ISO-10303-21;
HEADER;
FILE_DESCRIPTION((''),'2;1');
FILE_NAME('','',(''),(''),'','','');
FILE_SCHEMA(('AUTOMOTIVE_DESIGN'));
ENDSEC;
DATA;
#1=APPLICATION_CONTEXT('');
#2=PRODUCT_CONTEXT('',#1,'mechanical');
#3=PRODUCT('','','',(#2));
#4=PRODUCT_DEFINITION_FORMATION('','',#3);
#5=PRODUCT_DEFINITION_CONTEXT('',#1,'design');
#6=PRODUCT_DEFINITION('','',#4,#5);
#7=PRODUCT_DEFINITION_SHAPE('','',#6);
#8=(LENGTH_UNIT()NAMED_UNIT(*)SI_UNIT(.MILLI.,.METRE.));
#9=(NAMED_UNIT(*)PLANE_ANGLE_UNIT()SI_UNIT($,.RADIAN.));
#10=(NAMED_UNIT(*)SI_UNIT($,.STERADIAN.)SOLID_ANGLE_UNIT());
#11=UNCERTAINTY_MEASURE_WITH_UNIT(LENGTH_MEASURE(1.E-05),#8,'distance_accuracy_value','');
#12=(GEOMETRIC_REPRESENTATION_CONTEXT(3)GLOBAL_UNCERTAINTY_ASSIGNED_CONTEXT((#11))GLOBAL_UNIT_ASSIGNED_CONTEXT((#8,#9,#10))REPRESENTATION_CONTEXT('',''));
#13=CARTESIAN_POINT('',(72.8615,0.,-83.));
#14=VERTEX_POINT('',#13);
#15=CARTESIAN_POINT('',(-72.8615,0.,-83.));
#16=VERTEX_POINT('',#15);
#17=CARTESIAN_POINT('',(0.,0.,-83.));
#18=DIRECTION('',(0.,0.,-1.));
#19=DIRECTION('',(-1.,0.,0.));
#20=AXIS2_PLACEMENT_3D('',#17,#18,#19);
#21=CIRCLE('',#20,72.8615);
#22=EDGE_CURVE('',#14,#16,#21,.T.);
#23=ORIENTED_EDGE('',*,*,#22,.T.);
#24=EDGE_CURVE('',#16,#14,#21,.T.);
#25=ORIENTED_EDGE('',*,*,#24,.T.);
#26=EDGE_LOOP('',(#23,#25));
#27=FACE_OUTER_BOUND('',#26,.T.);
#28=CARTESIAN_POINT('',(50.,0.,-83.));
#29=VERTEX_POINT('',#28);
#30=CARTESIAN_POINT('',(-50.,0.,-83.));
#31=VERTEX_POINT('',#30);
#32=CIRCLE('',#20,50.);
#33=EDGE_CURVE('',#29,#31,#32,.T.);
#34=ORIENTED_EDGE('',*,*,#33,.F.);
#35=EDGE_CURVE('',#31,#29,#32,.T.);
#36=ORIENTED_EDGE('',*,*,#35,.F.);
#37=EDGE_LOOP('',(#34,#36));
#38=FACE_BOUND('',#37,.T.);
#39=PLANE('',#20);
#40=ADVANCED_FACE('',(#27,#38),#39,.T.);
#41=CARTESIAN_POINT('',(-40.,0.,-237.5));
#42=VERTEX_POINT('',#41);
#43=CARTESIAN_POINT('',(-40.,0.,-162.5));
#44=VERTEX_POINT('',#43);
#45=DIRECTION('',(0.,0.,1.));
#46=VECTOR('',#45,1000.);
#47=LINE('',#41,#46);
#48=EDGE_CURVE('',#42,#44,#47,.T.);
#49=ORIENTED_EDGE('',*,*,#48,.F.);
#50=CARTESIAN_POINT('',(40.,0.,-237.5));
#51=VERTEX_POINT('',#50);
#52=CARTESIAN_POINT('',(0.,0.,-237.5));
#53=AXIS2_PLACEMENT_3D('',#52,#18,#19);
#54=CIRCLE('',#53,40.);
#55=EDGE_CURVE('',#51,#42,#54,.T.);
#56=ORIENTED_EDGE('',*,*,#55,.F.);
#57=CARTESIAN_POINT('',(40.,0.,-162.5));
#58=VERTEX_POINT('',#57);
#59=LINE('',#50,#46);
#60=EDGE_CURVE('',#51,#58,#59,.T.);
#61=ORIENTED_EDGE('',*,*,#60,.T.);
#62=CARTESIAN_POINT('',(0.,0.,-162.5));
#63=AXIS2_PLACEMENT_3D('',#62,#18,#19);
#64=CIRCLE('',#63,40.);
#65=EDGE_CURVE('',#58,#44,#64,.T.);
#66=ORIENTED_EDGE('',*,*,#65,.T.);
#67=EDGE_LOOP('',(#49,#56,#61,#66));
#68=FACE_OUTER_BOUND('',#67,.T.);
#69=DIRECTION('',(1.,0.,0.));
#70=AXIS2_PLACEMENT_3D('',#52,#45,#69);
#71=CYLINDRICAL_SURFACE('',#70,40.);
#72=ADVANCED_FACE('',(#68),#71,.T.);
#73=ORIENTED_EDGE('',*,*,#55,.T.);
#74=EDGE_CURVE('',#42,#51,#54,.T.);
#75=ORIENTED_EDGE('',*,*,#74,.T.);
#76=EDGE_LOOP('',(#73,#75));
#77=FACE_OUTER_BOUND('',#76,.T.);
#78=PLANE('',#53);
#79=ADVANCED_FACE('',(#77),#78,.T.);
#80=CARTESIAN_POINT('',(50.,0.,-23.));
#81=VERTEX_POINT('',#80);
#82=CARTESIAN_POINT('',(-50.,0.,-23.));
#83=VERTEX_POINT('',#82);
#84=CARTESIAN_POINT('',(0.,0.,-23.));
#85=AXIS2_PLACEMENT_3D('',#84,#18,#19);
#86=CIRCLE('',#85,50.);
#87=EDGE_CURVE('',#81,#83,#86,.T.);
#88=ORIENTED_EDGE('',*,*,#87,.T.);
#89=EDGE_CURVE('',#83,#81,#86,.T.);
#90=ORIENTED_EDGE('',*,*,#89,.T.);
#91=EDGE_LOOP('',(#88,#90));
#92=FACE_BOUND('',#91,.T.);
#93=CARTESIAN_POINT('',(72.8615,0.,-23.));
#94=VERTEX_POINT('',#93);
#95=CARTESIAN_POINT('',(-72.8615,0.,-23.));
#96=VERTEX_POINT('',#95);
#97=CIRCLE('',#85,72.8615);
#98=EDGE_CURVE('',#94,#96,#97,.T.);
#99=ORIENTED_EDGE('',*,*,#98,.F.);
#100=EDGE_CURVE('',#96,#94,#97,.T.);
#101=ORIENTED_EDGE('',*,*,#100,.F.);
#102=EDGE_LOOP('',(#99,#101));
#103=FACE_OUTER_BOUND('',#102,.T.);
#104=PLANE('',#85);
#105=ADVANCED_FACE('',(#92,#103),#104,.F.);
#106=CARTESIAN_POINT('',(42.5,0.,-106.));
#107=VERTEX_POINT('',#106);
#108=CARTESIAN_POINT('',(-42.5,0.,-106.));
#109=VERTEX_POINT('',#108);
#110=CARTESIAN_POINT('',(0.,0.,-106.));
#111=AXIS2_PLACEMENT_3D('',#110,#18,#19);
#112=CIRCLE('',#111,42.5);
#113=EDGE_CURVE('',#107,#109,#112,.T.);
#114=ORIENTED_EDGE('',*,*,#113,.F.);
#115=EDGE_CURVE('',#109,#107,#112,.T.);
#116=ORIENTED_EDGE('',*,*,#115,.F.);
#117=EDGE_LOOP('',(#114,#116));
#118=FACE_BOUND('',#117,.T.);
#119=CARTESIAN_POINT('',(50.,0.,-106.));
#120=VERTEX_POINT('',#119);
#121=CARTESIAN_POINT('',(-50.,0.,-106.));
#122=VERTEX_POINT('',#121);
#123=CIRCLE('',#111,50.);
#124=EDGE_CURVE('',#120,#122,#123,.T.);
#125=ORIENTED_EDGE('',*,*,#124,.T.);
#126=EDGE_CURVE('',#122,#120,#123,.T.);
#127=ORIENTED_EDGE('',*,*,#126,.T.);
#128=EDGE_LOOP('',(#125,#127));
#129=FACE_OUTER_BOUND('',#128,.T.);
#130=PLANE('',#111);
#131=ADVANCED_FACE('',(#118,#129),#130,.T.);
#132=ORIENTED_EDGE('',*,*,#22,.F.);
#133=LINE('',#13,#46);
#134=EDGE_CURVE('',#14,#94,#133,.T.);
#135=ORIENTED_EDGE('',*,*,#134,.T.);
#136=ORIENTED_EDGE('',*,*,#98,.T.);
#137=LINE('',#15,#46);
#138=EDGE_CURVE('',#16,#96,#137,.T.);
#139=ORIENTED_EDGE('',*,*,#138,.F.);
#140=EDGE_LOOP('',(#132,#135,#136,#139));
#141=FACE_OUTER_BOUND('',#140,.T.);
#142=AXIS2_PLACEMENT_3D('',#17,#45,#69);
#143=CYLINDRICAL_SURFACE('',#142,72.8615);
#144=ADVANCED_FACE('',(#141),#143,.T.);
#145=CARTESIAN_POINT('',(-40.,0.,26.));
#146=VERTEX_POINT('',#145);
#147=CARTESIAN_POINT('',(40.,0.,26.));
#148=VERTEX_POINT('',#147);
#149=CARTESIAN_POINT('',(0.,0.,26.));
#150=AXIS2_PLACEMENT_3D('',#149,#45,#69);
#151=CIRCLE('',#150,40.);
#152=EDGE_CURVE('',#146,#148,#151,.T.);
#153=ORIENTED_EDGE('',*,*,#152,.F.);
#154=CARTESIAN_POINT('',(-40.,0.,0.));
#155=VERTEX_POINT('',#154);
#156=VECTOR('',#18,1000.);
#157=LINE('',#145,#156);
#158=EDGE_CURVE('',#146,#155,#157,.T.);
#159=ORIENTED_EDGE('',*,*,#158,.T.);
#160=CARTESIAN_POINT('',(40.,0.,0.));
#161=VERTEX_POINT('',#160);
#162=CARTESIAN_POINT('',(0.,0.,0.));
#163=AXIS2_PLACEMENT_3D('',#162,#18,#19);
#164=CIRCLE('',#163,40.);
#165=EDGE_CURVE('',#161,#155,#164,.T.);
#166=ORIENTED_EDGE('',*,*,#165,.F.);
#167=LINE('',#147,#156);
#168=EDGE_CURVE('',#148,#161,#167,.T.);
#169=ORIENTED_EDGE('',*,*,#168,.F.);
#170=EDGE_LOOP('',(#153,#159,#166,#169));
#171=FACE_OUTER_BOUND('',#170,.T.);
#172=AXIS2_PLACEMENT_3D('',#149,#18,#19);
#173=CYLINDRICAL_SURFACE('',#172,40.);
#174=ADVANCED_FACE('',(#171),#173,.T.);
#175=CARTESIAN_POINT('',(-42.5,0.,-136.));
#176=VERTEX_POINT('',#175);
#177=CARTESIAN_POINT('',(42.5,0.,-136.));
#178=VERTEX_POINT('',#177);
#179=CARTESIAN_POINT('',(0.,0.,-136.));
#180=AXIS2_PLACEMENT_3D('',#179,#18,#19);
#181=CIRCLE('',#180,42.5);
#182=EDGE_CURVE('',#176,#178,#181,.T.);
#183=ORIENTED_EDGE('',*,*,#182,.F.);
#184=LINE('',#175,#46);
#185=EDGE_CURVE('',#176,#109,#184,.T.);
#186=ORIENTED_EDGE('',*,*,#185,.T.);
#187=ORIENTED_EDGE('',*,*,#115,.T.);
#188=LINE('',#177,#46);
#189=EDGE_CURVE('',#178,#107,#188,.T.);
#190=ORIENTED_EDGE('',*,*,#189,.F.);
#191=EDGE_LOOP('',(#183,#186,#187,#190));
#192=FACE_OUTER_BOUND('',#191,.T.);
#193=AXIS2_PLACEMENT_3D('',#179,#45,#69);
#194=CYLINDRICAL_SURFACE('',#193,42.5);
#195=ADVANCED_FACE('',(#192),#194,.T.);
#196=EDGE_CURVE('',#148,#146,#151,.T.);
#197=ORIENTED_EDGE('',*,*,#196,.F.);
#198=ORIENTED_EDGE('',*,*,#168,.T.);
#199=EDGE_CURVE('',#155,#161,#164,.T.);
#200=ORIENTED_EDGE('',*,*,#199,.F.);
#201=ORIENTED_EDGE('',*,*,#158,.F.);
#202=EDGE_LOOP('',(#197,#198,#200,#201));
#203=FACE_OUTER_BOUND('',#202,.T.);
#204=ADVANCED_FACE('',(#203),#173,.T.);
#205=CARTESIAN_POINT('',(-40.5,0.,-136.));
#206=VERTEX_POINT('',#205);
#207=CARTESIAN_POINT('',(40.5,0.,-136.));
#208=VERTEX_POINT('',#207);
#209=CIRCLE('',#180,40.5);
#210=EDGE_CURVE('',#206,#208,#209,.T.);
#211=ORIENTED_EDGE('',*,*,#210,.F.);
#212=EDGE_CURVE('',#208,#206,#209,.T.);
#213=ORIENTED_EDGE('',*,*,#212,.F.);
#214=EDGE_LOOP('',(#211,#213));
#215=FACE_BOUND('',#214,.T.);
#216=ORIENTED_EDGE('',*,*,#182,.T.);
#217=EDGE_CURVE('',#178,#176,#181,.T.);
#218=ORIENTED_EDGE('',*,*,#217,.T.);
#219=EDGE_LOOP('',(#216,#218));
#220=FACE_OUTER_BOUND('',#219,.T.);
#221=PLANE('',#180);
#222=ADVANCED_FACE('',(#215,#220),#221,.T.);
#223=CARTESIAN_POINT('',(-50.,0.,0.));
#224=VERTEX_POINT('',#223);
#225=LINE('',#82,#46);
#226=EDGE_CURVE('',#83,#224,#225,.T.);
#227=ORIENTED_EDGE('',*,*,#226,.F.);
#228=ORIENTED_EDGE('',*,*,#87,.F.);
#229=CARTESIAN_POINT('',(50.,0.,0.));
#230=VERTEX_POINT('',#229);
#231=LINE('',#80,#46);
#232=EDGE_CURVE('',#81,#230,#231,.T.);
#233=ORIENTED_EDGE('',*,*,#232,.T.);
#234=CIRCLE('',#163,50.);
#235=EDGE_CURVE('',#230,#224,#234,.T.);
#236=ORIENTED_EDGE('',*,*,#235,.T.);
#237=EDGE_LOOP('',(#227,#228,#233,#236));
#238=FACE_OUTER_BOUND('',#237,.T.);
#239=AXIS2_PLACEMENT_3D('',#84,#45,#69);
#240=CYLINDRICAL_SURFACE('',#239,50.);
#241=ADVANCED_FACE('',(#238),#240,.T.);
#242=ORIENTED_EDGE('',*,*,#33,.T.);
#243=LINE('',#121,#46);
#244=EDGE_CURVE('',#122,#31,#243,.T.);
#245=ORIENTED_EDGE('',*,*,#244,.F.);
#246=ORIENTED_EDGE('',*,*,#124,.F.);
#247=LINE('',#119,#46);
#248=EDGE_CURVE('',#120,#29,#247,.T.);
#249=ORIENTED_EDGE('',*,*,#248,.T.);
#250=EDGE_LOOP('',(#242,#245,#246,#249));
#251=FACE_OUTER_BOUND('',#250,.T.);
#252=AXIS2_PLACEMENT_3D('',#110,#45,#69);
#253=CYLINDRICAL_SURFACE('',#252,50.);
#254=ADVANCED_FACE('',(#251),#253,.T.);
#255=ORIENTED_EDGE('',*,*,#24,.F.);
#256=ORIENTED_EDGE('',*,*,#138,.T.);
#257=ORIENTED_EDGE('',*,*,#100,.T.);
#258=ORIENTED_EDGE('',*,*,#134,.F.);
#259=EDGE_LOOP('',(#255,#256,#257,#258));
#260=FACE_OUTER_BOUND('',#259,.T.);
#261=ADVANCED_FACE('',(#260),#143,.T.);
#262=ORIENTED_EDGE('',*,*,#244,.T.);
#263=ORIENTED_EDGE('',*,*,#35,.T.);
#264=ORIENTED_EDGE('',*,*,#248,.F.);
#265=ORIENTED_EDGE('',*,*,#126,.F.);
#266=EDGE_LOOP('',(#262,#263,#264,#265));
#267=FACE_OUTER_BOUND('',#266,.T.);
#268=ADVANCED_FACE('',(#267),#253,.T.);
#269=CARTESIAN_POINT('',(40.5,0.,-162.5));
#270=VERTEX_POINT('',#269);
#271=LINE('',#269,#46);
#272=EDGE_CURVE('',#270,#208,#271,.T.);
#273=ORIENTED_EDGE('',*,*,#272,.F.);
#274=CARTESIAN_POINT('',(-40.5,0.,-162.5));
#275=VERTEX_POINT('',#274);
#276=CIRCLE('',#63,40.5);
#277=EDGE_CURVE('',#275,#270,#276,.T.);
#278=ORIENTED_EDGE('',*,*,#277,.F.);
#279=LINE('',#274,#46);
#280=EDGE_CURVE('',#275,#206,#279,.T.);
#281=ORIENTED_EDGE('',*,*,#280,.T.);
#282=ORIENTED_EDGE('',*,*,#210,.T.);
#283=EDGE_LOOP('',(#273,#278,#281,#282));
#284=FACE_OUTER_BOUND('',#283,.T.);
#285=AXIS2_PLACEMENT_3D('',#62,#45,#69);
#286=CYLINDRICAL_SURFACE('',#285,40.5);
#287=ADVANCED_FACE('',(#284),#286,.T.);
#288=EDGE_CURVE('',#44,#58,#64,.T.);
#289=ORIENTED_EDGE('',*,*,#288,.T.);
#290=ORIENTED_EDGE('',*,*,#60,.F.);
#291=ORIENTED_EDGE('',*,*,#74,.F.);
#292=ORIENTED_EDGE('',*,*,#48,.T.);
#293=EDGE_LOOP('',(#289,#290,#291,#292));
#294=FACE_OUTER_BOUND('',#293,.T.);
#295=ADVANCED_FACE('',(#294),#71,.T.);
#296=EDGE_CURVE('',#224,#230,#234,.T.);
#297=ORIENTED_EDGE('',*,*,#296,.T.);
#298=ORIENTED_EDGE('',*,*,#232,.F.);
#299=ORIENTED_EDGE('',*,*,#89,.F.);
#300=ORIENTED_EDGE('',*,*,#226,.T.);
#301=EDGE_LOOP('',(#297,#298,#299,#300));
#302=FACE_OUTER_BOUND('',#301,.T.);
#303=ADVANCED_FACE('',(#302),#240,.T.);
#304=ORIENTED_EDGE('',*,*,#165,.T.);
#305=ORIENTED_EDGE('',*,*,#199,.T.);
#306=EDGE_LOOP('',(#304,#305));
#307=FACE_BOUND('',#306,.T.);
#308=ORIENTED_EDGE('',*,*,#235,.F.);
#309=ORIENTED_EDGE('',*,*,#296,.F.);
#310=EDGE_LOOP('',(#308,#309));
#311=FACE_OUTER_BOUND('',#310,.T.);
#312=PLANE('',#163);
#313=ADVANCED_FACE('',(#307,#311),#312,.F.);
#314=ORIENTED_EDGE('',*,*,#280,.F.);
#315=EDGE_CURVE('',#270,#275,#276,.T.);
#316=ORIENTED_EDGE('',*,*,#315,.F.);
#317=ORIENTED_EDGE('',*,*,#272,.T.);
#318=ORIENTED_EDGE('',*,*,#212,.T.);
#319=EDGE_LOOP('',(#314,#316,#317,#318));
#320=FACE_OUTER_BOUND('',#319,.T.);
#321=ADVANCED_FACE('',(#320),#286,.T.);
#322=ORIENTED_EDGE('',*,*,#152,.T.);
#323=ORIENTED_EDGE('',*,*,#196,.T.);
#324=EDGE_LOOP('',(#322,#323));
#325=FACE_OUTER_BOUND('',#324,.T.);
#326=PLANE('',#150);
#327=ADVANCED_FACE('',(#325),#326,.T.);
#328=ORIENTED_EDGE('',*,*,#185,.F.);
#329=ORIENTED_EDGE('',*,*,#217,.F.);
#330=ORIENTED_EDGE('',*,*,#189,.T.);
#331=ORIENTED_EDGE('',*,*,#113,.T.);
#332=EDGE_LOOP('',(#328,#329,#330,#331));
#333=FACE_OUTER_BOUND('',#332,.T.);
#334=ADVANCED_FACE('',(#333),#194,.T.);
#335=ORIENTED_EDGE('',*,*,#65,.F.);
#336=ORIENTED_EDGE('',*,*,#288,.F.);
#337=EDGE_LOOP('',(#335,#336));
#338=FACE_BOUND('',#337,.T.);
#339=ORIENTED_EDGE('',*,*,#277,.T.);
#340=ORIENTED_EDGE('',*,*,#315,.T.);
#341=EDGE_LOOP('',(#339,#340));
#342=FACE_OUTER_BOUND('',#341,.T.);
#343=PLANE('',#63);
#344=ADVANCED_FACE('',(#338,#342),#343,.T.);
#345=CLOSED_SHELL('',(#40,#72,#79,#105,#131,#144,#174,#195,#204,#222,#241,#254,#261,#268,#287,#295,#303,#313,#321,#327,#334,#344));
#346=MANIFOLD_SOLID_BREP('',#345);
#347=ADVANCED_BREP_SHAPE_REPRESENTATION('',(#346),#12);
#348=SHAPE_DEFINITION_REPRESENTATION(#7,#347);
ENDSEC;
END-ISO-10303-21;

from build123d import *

# Parameters (mm, degrees)
SKETCH1_R           = 40
BOSS_EXTRUDE1_DEPTH = 26
SKETCH2_R           = 50
BOSS_EXTRUDE2_DEPTH = 23
SKETCH3_R           = 72.8615
BOSS_EXTRUDE3_DEPTH = 60
SKETCH4_R           = 50
BOSS_EXTRUDE4_DEPTH = 23
SKETCH6_R           = 42.5
BOSS_EXTRUDE5_DEPTH = 30
SKETCH7_R           = 40.5
BOSS_EXTRUDE6_DEPTH = 26.5
BOSS_EXTRUDE7_START = 75
SKETCH8_R           = 40
BOSS_EXTRUDE7_DEPTH = 75


with BuildPart() as part:
    # Sketch1 → Boss-Extrude1 (new body)
    with BuildSketch(Plane.XY):
        with Locations(Location((0, 0, 0), (0, 0, 180))):
            Circle(SKETCH1_R)
    extrude(amount=BOSS_EXTRUDE1_DEPTH)

    # Sketch2 → Boss-Extrude2 (add)
    with BuildSketch(Plane(origin=(0, 0, 0), x_dir=(-1, 0, 0), z_dir=(0, 0, -1))):
        Circle(SKETCH2_R)
    extrude(amount=BOSS_EXTRUDE2_DEPTH)

    # Sketch3 → Boss-Extrude3 (add)
    with BuildSketch(Plane(origin=(0, 0, -23), x_dir=(-1, 0, 0), z_dir=(0, 0, -1))):
        Circle(SKETCH3_R)
    extrude(amount=BOSS_EXTRUDE3_DEPTH)

    # Sketch4 → Boss-Extrude4 (add)
    with BuildSketch(Plane(origin=(0, 0, -83), x_dir=(-1, 0, 0), z_dir=(0, 0, -1))):
        Circle(SKETCH4_R)
    extrude(amount=BOSS_EXTRUDE4_DEPTH)

    # Sketch6 → Boss-Extrude5 (add)
    with BuildSketch(Plane(origin=(0, 0, -106), x_dir=(-1, 0, 0), z_dir=(0, 0, -1))):
        Circle(SKETCH6_R)
    extrude(amount=BOSS_EXTRUDE5_DEPTH)

    # Sketch7 → Boss-Extrude6 (add)
    with BuildSketch(Plane(origin=(0, 0, -136), x_dir=(-1, 0, 0), z_dir=(0, 0, -1))):
        Circle(SKETCH7_R)
    extrude(amount=BOSS_EXTRUDE6_DEPTH)

    # Sketch8 → Boss-Extrude7 (add)
    with BuildSketch(Plane(origin=(0, 0, -162.5), x_dir=(-1, 0, 0), z_dir=(0, 0, -1)).offset(BOSS_EXTRUDE7_START)):
        Circle(SKETCH8_R)
    extrude(amount=-BOSS_EXTRUDE7_DEPTH)


solid = part.part
